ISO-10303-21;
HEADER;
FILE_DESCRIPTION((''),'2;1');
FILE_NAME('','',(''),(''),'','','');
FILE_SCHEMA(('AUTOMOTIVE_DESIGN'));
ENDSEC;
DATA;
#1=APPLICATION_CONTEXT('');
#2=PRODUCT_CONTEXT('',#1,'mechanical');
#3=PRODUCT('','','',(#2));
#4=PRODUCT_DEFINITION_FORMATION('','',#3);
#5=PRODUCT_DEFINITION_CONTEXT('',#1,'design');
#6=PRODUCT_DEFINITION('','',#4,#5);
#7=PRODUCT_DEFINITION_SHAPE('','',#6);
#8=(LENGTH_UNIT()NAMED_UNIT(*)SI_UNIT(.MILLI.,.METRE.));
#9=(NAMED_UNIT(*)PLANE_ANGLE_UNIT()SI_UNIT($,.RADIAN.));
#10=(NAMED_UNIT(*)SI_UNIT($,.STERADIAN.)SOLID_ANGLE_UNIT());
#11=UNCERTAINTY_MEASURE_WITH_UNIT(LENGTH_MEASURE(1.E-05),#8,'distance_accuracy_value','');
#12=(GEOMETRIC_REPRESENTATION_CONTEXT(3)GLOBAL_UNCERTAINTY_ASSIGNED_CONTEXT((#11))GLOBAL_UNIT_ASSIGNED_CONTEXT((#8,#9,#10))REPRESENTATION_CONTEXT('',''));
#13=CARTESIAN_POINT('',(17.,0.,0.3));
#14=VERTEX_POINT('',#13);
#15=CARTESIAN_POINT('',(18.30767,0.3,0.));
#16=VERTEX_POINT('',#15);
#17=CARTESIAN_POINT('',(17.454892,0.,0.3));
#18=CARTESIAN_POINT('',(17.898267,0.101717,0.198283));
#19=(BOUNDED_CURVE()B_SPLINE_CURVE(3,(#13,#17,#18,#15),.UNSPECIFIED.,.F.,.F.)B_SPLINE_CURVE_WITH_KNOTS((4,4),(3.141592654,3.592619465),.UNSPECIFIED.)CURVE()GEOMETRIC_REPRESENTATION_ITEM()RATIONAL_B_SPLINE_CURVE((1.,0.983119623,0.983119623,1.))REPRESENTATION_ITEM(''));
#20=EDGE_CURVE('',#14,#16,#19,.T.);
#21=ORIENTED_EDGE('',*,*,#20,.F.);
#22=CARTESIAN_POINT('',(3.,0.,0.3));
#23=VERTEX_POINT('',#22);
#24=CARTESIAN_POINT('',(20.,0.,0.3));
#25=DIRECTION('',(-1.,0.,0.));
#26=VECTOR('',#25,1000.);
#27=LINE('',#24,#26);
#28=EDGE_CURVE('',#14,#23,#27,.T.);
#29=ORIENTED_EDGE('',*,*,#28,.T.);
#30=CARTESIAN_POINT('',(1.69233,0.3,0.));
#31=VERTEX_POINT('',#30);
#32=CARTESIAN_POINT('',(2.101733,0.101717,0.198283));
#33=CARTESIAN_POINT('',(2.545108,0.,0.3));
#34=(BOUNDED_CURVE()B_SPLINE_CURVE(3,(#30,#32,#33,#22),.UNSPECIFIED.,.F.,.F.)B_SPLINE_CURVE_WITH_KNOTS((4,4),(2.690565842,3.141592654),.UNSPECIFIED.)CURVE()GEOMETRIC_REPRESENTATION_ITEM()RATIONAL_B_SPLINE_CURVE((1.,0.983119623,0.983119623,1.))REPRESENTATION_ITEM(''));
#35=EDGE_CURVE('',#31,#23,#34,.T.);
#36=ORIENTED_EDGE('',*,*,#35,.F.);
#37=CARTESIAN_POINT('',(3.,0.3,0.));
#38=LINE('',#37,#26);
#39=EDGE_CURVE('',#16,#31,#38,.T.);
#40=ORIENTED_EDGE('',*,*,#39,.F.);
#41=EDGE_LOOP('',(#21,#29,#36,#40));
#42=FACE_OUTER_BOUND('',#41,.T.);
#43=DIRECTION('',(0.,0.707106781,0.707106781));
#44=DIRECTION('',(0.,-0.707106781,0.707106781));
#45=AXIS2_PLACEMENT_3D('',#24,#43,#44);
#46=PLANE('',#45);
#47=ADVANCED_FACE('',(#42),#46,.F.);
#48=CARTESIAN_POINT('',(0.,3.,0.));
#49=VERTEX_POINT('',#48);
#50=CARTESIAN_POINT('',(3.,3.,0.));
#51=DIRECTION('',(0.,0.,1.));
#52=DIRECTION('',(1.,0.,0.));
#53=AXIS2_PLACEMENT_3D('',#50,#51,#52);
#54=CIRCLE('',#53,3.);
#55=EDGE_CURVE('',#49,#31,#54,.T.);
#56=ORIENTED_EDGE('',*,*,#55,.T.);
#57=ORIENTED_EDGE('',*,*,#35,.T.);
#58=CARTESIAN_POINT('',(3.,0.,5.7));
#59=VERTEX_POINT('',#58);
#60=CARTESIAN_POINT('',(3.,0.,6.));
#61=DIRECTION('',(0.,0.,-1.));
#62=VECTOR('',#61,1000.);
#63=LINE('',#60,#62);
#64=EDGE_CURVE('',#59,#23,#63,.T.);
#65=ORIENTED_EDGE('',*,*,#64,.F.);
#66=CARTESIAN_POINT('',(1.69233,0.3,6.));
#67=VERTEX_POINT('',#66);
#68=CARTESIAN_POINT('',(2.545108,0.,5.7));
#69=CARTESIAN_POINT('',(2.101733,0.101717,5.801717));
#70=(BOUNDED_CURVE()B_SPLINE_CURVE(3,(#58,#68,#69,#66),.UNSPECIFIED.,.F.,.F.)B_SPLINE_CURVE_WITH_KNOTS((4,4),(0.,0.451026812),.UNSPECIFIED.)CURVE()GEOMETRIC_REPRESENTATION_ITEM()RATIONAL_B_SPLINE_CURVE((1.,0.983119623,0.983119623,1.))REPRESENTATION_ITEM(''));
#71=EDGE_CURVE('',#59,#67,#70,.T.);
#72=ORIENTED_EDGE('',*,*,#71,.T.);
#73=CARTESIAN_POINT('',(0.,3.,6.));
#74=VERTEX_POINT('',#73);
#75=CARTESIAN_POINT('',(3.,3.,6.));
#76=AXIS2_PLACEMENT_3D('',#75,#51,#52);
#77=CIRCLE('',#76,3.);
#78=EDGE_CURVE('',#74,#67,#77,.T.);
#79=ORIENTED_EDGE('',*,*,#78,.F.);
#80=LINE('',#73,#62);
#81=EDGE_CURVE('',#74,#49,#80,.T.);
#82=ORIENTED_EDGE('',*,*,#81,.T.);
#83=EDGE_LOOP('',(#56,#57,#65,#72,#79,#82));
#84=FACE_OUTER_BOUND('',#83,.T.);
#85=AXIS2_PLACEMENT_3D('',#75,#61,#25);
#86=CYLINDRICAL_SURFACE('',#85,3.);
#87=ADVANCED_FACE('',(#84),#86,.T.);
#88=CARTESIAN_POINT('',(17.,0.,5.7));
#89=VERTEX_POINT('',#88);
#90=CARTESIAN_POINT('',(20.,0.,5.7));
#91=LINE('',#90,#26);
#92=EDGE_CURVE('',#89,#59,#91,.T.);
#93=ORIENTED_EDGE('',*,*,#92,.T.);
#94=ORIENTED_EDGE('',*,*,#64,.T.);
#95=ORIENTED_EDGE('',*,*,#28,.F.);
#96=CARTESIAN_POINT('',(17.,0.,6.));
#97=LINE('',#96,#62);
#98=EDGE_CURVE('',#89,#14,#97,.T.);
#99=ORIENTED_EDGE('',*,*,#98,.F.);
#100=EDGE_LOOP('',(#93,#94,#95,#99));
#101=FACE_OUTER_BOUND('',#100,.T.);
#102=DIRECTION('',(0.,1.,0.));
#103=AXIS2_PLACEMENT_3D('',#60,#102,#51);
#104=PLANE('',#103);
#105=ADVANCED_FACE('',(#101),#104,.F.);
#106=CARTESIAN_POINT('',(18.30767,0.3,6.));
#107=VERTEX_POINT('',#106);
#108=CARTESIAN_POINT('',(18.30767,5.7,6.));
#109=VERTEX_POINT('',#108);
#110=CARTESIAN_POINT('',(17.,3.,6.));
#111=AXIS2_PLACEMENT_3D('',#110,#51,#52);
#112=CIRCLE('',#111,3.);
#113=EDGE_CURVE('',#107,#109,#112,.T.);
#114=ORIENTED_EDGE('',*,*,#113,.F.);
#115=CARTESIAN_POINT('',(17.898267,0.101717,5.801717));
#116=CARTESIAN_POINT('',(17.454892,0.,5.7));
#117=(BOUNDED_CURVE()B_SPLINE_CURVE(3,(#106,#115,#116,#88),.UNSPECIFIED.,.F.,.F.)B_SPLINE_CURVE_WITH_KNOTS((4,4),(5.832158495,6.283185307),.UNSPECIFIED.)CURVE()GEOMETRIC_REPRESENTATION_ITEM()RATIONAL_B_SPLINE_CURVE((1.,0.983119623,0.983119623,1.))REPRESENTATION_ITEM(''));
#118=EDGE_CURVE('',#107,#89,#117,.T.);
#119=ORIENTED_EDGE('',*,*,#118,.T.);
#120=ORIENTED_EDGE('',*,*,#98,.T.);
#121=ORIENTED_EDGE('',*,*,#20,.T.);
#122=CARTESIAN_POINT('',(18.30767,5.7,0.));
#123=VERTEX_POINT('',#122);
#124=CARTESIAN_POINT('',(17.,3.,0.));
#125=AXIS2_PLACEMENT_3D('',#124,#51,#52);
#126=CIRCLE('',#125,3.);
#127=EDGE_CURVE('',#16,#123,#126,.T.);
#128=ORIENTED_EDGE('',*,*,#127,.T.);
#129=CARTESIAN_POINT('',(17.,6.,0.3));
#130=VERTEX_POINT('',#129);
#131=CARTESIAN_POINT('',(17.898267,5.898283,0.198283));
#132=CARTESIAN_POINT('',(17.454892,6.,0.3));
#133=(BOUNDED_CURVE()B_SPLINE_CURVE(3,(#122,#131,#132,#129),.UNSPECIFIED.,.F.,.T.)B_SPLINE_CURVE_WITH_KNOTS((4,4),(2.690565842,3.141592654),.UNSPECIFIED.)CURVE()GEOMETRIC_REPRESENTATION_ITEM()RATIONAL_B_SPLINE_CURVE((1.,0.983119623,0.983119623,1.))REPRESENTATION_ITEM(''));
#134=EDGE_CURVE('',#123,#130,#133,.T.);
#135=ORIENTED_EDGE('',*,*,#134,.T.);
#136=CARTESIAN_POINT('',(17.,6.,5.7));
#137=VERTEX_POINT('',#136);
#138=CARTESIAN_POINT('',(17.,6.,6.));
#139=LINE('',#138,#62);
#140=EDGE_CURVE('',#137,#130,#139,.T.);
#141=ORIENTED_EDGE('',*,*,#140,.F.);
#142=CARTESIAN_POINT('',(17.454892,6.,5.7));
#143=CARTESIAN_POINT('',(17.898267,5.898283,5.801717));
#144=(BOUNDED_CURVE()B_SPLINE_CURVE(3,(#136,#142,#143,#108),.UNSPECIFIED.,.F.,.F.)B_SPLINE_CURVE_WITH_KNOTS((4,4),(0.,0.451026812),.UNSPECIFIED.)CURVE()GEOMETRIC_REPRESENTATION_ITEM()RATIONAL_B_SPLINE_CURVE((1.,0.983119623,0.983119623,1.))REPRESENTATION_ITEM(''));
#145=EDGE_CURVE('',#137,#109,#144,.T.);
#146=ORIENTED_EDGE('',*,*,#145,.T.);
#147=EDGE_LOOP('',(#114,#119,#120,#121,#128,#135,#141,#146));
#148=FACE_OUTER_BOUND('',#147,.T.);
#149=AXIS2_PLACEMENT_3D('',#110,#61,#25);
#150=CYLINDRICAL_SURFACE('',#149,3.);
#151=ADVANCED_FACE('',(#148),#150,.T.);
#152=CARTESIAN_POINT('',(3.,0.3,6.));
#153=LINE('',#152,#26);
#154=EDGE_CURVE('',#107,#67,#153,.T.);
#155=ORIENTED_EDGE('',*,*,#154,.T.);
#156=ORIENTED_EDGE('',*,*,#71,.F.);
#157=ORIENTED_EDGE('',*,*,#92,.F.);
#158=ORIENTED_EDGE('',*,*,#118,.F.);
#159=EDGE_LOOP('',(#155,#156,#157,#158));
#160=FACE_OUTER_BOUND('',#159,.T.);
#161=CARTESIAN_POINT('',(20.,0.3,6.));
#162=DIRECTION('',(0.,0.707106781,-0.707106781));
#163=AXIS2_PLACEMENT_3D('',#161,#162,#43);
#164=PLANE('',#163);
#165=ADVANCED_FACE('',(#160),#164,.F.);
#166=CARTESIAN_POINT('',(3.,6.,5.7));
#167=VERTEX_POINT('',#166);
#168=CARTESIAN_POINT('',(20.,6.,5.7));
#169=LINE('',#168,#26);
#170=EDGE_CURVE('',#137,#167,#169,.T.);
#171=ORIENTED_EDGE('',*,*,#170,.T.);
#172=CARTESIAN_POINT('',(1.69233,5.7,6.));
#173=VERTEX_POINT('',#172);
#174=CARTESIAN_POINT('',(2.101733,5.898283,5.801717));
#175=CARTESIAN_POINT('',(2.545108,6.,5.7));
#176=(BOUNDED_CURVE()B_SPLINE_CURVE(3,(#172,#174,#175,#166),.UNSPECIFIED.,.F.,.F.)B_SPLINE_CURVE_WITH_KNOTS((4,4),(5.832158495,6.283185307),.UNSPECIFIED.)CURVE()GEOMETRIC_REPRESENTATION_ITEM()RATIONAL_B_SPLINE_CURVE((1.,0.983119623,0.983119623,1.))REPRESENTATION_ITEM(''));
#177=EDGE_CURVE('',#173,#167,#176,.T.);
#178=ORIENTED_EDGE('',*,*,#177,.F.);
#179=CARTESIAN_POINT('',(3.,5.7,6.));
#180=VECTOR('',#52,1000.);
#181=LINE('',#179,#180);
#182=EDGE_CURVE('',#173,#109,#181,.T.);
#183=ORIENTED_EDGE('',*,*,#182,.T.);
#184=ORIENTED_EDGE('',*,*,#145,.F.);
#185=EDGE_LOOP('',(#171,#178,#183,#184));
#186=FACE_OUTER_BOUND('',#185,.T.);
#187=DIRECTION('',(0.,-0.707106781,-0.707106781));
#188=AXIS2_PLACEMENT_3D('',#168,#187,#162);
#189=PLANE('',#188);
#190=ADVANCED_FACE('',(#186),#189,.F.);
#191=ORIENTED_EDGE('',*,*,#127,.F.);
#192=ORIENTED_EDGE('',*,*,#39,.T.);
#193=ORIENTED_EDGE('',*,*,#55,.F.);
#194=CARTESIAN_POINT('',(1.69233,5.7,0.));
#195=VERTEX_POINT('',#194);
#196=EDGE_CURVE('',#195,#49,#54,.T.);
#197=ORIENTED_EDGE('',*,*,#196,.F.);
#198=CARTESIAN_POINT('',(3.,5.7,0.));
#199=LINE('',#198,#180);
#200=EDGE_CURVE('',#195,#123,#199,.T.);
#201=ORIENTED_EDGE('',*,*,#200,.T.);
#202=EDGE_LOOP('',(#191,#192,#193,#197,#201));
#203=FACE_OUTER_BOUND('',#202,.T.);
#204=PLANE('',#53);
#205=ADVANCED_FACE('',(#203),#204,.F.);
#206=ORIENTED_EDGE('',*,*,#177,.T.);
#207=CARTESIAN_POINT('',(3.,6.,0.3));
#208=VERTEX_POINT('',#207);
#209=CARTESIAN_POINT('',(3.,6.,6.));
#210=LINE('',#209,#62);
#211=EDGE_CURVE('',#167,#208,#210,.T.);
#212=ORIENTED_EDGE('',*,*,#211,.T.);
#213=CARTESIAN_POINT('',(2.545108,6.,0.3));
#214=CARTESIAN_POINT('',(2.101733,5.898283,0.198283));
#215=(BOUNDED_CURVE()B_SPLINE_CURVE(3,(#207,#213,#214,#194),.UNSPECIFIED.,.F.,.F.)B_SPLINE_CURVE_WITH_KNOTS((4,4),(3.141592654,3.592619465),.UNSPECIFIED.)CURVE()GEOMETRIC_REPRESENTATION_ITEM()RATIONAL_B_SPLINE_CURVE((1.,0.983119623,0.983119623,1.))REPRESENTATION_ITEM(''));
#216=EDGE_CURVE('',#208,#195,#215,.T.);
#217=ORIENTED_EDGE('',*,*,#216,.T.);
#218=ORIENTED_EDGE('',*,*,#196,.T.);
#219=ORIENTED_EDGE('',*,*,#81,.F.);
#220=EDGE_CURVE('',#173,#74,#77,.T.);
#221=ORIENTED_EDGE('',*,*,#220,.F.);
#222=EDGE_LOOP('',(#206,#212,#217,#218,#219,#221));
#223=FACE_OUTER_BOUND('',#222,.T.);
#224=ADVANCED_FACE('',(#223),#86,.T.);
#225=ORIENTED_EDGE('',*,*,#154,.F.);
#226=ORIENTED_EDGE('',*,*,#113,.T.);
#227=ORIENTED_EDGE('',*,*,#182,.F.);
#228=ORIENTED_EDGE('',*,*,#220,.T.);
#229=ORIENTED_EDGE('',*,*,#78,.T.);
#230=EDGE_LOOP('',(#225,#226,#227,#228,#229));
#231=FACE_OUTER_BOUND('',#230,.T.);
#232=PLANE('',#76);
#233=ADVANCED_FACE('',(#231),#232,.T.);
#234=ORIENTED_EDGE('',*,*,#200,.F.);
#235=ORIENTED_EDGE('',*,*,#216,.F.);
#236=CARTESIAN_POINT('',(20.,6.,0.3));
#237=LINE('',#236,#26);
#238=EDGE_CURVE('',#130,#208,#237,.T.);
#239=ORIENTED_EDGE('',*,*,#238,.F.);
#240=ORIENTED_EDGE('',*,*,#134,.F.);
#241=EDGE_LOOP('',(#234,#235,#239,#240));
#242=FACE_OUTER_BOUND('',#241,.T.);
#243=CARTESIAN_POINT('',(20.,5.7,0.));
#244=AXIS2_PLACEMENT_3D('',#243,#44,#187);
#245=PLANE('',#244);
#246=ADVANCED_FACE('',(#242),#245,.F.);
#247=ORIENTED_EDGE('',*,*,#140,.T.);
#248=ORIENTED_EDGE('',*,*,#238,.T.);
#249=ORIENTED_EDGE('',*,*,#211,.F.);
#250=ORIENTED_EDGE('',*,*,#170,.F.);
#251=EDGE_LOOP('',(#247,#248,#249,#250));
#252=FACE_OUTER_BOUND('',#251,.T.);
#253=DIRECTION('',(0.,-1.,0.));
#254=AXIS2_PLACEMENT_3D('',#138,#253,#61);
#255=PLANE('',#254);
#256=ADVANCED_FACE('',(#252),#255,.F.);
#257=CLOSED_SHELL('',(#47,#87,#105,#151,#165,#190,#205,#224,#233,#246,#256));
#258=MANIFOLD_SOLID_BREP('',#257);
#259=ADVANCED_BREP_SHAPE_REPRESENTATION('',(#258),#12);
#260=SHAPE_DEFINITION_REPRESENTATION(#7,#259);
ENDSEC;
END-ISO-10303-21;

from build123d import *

# Parameters (mm, degrees)
EXTRUDE_1_DEPTH     = 6
SKETCH_2_W          = 12
SKETCH_2_H          = 12
CUT_EXTRUDE_1_DEPTH = 20


with BuildPart() as part:
    # 草图1 → 凸台-拉伸1 (new body)
    with BuildSketch(Plane.XY):
        with BuildLine():
            Line((3, 0), (17, 0))
            ThreePointArc((17, 0), (19.121320344, 0.878679656), (20, 3))
            ThreePointArc((20, 3), (19.121320344, 5.121320344), (17, 6))
            Line((17, 6), (3, 6))
            ThreePointArc((3, 6), (0.878679656, 5.121320344), (0, 3))
            ThreePointArc((0, 3), (0.878679656, 0.878679656), (3, 0))
        make_face()
    extrude(amount=EXTRUDE_1_DEPTH)

    # 草图2 → 切除-拉伸1 (cut)
    with BuildSketch(Plane(origin=(0, 0, 0), x_dir=(0, 0, -1), z_dir=(1, 0, 0))):
        with Locations((-3, 3)):
            Rectangle(SKETCH_2_W, SKETCH_2_H)
        Polygon((-6, 5.7), (-6, 0.3), (-5.7, 0), (-0.3, 0), (0, 0.3), (0, 5.7), (-0.3, 6), (-5.7, 6), align=None, mode=Mode.SUBTRACT)
    extrude(amount=CUT_EXTRUDE_1_DEPTH, mode=Mode.SUBTRACT)


solid = part.part
